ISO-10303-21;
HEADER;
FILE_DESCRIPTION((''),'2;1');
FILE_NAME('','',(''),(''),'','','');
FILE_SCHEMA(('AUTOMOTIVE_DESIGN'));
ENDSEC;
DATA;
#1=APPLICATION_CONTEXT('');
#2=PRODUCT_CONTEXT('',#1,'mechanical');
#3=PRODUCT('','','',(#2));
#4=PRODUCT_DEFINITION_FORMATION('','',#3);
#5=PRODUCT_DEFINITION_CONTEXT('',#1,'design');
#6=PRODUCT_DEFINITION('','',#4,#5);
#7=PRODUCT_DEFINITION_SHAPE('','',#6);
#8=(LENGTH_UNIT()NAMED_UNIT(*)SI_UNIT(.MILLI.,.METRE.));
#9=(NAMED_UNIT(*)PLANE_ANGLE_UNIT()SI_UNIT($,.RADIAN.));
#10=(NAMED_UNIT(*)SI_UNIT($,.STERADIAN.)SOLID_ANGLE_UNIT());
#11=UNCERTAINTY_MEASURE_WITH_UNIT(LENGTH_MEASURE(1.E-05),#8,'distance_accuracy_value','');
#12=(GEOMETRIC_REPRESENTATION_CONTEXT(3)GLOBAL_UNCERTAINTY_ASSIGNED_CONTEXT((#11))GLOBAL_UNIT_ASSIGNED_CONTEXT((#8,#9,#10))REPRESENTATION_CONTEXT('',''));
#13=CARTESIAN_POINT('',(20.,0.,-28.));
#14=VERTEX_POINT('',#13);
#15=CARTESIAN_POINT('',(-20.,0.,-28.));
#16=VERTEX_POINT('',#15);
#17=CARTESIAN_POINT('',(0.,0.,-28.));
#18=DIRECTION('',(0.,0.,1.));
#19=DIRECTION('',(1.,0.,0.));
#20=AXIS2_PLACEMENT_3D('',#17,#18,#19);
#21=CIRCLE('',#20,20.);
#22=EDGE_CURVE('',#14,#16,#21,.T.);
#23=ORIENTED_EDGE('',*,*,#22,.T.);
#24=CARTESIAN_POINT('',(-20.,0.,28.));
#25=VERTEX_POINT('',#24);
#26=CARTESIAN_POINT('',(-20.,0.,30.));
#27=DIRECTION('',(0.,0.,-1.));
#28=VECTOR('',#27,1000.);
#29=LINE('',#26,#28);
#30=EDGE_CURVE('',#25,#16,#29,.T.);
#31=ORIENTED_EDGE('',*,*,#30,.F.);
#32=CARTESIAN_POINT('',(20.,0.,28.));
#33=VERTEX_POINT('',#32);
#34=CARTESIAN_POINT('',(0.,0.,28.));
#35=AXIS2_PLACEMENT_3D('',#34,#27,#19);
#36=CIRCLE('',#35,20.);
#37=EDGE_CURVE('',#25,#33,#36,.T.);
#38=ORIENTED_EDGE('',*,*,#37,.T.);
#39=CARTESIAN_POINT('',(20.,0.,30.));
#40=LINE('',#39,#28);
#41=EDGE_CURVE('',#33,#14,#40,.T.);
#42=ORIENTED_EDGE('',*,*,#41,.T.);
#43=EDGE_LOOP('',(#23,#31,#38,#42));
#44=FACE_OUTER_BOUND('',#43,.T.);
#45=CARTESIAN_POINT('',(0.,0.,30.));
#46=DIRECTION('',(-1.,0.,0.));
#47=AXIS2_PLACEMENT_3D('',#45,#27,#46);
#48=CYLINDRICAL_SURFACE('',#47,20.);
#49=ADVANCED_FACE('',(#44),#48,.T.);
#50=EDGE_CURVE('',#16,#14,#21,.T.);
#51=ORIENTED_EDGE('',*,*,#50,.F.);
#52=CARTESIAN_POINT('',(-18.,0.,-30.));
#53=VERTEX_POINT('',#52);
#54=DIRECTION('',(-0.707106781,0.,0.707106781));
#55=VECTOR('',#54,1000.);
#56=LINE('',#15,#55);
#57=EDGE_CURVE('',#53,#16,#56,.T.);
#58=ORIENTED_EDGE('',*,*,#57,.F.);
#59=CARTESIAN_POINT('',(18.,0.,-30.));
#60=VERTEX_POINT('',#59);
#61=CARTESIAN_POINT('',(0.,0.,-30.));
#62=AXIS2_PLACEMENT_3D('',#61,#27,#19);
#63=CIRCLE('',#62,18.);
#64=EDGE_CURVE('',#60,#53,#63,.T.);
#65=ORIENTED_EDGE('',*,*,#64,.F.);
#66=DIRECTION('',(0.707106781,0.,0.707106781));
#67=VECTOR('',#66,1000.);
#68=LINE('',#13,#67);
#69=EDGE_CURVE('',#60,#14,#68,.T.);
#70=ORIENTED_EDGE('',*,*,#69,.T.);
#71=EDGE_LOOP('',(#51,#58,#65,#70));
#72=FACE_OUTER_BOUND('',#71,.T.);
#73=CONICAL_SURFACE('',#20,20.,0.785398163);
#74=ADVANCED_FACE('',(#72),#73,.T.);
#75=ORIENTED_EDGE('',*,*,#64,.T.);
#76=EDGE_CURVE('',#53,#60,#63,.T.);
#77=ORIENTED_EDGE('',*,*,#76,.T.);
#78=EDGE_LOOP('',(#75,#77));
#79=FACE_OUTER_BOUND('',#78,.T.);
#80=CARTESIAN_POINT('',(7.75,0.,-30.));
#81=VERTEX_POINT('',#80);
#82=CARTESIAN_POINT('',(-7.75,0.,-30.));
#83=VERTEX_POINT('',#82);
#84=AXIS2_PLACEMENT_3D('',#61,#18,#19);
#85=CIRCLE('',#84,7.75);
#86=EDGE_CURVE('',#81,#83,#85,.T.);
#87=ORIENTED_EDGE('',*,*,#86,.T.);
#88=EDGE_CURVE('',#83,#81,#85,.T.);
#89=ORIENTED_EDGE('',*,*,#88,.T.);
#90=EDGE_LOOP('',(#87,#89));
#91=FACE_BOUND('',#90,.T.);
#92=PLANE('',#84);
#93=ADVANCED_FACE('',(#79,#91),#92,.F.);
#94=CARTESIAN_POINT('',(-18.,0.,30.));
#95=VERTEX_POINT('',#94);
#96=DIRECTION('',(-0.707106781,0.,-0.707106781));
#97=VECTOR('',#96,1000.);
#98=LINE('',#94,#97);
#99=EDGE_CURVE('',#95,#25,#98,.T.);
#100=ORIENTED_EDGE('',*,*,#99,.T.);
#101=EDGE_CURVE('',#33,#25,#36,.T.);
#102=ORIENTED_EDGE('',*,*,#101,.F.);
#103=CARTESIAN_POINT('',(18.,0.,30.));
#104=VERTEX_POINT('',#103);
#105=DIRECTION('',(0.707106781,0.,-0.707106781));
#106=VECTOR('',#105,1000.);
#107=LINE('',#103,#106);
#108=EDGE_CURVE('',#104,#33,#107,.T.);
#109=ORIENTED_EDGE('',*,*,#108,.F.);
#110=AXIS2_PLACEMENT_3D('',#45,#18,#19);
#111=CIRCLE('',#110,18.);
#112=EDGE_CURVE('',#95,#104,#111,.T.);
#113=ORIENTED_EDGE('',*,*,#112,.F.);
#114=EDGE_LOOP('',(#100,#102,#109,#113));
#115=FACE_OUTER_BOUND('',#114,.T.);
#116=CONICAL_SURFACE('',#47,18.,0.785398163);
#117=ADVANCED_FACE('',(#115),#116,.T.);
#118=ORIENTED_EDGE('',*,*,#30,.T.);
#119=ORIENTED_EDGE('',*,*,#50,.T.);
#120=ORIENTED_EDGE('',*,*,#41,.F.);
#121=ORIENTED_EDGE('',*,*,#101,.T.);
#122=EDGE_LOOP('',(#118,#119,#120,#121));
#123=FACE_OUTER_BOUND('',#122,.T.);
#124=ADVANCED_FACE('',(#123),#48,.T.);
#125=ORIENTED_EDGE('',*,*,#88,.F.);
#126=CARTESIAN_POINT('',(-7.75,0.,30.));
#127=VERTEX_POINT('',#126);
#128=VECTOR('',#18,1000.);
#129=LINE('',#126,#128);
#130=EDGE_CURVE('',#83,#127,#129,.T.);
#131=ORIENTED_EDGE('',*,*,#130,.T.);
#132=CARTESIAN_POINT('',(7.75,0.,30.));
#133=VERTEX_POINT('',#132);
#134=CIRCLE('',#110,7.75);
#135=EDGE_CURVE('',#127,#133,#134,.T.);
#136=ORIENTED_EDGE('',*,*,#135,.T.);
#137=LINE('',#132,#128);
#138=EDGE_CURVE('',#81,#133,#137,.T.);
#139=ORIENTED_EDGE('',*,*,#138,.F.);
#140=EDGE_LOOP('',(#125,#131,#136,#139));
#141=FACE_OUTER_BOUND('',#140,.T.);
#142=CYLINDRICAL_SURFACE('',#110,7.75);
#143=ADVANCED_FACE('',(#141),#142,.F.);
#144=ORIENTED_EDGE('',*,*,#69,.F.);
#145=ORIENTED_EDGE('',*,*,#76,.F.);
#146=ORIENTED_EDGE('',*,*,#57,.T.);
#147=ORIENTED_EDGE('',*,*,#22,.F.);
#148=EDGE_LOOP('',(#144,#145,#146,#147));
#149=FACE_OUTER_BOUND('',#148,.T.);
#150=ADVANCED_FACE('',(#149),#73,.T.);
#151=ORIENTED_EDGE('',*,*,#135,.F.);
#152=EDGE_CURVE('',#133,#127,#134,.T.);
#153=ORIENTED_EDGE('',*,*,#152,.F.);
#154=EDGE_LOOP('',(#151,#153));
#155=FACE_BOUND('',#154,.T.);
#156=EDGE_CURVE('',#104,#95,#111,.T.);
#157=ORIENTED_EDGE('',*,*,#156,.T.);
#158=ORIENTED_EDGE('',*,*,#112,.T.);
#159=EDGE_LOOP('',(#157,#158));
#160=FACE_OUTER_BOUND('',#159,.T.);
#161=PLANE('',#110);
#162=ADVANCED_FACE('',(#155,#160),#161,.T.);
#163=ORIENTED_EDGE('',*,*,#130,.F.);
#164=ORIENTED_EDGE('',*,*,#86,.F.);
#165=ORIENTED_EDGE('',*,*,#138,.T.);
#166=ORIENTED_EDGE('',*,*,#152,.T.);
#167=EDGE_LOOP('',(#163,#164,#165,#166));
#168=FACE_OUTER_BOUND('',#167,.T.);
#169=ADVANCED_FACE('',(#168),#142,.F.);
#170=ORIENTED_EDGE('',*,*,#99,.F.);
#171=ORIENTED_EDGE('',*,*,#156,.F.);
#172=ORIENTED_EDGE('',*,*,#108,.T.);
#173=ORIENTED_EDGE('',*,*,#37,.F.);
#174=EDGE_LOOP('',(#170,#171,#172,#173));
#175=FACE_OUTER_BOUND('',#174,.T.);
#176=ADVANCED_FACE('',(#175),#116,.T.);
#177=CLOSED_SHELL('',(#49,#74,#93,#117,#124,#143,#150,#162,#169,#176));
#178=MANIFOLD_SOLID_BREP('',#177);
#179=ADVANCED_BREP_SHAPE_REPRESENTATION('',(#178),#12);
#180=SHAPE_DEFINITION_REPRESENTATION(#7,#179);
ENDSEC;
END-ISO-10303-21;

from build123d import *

# Parameters (mm, degrees)
SKETCH1_R           = 20
BOSS_EXTRUDE1_DEPTH = 30
CHAMFER1_SIZE       = 2
M18_TAPPED_HOLE1_D  = 15.5


with BuildPart() as part:
    # Sketch1 → Boss-Extrude1 (new, symmetric)
    with BuildSketch(Plane.XY):
        Circle(SKETCH1_R)
    extrude(amount=BOSS_EXTRUDE1_DEPTH, both=True)

    # Chamfer1
    chamfer1_edges = [part.edges().sort_by_distance(p)[0] for p in [
        (-20, 0, -30),
        (-20, 0, 30),
    ]]
    chamfer(chamfer1_edges, length=CHAMFER1_SIZE)

    # M18 Tapped Hole1 (through all)
    with Locations(Plane.XY.offset(30)):
        with Locations((0, 0)):
            Hole(M18_TAPPED_HOLE1_D / 2)


solid = part.part
